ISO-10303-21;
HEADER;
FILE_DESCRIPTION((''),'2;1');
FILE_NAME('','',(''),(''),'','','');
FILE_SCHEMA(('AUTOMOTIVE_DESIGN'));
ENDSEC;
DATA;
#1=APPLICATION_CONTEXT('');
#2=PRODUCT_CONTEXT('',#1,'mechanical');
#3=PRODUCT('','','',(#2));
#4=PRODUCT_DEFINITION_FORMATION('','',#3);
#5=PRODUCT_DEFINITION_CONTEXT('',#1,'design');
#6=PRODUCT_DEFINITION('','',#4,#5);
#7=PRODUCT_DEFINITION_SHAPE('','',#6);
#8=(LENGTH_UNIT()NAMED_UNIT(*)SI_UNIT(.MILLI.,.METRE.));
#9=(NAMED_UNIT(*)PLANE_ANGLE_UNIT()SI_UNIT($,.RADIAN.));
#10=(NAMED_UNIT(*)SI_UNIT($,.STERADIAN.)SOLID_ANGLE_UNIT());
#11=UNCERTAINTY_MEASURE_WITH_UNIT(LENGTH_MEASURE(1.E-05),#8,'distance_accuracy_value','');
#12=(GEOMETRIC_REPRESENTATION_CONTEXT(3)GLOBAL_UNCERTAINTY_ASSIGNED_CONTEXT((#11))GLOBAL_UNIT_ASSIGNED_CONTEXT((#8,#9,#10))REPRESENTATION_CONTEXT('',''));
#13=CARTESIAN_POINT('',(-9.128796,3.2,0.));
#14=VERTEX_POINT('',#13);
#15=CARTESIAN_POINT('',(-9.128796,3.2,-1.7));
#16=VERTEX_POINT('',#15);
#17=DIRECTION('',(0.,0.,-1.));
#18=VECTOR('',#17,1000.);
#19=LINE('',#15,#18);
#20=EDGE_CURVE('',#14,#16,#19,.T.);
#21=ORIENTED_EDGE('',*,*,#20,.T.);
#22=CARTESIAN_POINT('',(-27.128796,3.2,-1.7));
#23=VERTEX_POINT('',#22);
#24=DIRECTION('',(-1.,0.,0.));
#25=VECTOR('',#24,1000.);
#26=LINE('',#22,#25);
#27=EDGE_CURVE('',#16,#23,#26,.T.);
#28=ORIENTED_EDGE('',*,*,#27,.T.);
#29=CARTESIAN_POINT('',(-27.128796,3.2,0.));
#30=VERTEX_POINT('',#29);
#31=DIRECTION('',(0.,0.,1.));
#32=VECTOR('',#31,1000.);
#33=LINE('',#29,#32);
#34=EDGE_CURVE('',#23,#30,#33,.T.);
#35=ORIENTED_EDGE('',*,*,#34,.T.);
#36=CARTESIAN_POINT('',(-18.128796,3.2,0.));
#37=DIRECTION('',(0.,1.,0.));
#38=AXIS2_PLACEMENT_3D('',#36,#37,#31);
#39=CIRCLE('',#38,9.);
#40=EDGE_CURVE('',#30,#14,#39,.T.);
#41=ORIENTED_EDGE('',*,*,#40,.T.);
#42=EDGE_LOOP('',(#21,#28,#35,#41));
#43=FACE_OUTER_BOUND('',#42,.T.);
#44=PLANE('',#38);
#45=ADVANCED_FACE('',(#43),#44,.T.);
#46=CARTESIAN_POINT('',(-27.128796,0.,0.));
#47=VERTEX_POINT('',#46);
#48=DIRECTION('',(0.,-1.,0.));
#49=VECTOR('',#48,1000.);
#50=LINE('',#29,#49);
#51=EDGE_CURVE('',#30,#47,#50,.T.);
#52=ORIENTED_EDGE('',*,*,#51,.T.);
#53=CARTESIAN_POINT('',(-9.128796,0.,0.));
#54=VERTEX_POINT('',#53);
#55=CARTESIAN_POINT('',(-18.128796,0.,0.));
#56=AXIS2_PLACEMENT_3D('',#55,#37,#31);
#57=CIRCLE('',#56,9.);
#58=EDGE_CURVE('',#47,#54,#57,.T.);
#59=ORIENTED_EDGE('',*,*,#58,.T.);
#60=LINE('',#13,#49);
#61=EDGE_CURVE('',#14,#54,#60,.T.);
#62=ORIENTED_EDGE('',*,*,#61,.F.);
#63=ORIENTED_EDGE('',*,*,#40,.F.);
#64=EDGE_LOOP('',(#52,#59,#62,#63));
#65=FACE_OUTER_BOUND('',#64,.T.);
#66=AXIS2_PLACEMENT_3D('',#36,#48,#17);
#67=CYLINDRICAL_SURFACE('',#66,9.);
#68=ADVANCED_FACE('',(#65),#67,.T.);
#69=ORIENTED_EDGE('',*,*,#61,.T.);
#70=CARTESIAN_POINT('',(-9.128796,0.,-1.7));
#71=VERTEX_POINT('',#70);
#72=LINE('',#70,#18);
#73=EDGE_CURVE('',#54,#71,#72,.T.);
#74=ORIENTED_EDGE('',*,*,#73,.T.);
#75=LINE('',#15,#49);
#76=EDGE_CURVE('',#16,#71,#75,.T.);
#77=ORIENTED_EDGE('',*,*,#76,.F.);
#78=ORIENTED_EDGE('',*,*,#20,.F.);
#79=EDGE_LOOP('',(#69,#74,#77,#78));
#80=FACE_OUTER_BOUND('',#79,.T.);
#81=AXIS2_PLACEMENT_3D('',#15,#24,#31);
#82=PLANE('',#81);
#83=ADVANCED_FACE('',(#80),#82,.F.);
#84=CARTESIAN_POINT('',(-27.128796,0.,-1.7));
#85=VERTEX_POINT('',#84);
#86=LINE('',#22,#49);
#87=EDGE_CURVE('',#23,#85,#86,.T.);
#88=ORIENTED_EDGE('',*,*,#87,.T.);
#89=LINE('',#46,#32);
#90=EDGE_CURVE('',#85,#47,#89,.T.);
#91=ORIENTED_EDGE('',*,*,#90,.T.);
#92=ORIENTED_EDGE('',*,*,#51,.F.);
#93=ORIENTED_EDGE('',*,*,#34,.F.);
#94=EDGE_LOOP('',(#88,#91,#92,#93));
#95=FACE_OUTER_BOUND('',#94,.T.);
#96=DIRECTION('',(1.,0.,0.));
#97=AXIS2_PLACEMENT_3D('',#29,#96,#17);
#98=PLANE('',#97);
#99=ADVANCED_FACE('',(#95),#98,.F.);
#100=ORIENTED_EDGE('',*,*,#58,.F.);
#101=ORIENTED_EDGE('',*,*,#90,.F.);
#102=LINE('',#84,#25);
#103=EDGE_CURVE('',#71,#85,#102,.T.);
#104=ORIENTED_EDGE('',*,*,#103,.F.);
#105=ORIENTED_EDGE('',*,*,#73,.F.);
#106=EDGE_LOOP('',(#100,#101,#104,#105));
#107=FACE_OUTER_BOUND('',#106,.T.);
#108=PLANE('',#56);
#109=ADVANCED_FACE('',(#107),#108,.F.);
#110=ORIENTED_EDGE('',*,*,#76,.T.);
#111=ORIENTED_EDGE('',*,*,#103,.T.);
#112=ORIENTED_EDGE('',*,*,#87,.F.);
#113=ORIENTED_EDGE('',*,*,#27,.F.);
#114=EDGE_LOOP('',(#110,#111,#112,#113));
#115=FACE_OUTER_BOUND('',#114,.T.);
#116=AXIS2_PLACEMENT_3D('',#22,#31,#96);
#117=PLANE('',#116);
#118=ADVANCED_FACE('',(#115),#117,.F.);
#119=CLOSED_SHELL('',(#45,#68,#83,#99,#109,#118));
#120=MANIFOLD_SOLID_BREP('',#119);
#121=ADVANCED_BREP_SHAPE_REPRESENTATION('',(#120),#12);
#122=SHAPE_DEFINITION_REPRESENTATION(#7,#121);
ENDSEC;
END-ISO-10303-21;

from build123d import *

# Parameters (mm, degrees)
EXTRUDE1_DEPTH = 3.2


with BuildPart() as part:
    # Sketch1 → Extrude1 (new body)
    with BuildSketch(Plane(origin=(0, 0, 0), x_dir=(1, 0, 0), z_dir=(0, 1, 0))):
        with BuildLine():
            Line((-27.128795812, 0), (-27.128795812, 1.7))
            Line((-27.128795812, 1.7), (-9.128795812, 1.7))
            Line((-9.128795812, 1.7), (-9.128795812, 0))
            ThreePointArc((-9.128795812, 0), (-18.128795812, -9), (-27.128795812, 0))
        make_face()
    extrude(amount=EXTRUDE1_DEPTH)


solid = part.part
